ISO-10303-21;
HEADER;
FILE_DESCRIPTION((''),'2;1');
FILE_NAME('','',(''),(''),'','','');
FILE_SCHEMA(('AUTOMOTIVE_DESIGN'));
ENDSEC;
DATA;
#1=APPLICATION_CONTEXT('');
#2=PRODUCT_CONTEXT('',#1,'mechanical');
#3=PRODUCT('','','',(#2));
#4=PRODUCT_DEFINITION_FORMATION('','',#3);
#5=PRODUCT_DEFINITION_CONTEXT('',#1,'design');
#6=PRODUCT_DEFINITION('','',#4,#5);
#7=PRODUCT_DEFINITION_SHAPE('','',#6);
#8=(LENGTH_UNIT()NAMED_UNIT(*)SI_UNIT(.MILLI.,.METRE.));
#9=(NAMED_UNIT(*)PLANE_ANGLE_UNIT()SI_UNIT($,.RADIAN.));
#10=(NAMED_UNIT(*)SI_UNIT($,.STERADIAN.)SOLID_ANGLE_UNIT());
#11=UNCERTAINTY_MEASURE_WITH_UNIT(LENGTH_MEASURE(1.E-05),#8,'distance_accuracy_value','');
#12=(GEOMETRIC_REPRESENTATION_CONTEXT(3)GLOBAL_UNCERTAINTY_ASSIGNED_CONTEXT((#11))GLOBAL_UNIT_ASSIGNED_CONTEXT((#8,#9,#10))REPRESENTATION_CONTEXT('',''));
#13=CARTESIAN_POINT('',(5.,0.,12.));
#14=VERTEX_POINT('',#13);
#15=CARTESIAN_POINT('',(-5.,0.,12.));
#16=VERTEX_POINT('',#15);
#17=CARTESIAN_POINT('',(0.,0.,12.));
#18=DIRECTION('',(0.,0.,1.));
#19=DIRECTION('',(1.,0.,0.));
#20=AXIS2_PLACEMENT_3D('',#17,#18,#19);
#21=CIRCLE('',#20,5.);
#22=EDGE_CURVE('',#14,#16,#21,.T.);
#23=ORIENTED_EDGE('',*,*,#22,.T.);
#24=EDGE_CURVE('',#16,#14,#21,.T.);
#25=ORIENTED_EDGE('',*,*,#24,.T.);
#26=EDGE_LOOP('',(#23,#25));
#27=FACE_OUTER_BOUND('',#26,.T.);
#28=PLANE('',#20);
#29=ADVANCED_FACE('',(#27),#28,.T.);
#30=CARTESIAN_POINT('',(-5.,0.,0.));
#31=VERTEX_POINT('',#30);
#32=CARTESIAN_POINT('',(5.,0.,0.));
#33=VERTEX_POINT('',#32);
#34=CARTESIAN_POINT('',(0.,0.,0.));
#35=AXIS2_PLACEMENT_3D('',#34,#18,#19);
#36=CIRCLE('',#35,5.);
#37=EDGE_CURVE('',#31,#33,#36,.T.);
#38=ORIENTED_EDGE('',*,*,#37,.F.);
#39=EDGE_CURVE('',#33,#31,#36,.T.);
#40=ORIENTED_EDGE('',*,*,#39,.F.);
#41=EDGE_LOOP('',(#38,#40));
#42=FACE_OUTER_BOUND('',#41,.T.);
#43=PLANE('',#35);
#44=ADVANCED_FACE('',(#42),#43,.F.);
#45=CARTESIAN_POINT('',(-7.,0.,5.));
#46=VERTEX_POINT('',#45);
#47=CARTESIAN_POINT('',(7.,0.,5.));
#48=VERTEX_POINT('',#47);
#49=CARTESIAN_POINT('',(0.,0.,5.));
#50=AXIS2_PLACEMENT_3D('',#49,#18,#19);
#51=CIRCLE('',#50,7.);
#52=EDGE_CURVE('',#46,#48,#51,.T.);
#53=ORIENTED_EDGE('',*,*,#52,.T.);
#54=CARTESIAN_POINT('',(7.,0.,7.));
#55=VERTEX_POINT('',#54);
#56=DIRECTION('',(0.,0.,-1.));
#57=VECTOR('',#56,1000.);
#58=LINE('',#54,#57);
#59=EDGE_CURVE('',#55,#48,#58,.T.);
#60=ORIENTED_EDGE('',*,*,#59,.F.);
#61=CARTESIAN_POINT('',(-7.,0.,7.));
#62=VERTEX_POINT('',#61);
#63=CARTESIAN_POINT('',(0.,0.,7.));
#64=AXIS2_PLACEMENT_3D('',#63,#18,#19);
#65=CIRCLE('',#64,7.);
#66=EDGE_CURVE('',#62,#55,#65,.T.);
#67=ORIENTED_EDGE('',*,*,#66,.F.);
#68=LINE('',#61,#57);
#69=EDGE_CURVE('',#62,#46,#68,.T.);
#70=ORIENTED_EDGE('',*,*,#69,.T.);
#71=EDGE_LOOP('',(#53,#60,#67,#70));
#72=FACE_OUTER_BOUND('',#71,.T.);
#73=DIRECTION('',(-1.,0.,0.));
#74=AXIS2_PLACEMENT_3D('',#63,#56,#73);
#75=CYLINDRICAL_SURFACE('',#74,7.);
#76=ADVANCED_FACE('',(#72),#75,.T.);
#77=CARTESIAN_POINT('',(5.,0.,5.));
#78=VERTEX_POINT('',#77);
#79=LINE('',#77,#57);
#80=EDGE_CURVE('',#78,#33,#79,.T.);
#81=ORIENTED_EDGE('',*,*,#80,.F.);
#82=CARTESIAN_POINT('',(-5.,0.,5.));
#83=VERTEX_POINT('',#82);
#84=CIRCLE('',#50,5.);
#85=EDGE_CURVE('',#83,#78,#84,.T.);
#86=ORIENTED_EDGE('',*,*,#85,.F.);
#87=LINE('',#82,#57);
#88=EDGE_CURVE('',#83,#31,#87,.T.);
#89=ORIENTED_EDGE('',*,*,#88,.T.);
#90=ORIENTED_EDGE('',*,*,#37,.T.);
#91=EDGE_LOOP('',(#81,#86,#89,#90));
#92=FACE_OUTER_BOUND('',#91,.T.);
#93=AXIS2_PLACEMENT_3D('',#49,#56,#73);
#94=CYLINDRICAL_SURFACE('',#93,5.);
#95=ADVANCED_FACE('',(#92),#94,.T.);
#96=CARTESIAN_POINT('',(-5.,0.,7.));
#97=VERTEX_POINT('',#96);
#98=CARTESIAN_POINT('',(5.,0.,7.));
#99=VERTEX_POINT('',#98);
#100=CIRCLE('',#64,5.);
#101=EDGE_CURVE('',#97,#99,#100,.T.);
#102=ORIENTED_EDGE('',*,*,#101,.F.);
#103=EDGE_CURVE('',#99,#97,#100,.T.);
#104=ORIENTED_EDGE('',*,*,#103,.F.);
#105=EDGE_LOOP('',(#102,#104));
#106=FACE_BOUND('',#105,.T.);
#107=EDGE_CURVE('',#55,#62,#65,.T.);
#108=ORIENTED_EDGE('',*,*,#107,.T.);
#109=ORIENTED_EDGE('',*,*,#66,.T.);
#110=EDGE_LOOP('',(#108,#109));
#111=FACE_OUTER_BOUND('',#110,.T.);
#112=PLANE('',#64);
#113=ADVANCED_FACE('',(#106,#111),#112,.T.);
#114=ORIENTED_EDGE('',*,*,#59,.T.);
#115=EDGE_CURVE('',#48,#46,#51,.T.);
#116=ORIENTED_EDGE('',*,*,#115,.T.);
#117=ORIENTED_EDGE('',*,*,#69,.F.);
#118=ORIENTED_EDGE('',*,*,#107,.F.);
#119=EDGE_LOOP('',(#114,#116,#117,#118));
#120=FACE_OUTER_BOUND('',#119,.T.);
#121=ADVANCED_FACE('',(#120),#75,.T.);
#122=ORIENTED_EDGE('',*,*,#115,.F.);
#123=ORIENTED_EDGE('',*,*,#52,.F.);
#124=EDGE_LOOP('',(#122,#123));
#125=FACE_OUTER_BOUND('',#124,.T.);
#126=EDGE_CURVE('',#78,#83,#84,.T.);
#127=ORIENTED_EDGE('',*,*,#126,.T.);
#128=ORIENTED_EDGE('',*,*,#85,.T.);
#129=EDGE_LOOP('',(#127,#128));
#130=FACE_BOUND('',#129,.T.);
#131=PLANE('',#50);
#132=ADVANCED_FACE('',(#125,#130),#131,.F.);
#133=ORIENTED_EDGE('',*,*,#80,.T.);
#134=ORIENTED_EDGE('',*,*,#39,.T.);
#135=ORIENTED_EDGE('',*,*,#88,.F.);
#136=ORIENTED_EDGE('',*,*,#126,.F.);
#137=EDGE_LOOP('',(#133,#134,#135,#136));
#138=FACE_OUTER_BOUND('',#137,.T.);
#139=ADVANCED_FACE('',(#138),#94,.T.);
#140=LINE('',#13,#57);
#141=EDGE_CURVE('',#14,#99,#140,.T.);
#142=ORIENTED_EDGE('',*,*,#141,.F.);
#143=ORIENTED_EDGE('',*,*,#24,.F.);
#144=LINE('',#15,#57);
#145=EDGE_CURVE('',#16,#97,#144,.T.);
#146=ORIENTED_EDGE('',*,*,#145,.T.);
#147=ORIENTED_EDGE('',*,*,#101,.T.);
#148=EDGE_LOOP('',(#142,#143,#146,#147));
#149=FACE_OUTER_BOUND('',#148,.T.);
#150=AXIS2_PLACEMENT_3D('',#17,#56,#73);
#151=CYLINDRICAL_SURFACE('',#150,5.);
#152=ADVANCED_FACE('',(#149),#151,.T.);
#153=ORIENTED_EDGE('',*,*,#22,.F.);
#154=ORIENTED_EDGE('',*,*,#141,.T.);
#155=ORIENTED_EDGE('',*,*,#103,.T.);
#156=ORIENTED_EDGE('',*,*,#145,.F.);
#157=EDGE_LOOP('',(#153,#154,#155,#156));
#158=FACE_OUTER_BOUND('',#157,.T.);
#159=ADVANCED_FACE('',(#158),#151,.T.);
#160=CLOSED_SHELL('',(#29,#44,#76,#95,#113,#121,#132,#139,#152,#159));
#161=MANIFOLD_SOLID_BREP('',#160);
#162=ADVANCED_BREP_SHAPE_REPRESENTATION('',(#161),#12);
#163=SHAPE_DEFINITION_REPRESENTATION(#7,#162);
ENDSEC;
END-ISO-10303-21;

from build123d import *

# Parameters (mm, degrees)
SKETCH1_R           = 5
BOSS_EXTRUDE1_DEPTH = 5
SKETCH2_R           = 7
BOSS_EXTRUDE2_DEPTH = 2
SKETCH4_R           = 5
BOSS_EXTRUDE3_DEPTH = 5


with BuildPart() as part:
    # Sketch1 → Boss-Extrude1 (new body)
    with BuildSketch(Plane.XY):
        Circle(SKETCH1_R)
    extrude(amount=BOSS_EXTRUDE1_DEPTH)

    # Sketch2 → Boss-Extrude2 (add)
    with BuildSketch(Plane.XY.offset(5)):
        Circle(SKETCH2_R)
    extrude(amount=BOSS_EXTRUDE2_DEPTH)

    # Sketch4 → Boss-Extrude3 (add)
    with BuildSketch(Plane.XY.offset(7)):
        Circle(SKETCH4_R)
    extrude(amount=BOSS_EXTRUDE3_DEPTH)


solid = part.part
